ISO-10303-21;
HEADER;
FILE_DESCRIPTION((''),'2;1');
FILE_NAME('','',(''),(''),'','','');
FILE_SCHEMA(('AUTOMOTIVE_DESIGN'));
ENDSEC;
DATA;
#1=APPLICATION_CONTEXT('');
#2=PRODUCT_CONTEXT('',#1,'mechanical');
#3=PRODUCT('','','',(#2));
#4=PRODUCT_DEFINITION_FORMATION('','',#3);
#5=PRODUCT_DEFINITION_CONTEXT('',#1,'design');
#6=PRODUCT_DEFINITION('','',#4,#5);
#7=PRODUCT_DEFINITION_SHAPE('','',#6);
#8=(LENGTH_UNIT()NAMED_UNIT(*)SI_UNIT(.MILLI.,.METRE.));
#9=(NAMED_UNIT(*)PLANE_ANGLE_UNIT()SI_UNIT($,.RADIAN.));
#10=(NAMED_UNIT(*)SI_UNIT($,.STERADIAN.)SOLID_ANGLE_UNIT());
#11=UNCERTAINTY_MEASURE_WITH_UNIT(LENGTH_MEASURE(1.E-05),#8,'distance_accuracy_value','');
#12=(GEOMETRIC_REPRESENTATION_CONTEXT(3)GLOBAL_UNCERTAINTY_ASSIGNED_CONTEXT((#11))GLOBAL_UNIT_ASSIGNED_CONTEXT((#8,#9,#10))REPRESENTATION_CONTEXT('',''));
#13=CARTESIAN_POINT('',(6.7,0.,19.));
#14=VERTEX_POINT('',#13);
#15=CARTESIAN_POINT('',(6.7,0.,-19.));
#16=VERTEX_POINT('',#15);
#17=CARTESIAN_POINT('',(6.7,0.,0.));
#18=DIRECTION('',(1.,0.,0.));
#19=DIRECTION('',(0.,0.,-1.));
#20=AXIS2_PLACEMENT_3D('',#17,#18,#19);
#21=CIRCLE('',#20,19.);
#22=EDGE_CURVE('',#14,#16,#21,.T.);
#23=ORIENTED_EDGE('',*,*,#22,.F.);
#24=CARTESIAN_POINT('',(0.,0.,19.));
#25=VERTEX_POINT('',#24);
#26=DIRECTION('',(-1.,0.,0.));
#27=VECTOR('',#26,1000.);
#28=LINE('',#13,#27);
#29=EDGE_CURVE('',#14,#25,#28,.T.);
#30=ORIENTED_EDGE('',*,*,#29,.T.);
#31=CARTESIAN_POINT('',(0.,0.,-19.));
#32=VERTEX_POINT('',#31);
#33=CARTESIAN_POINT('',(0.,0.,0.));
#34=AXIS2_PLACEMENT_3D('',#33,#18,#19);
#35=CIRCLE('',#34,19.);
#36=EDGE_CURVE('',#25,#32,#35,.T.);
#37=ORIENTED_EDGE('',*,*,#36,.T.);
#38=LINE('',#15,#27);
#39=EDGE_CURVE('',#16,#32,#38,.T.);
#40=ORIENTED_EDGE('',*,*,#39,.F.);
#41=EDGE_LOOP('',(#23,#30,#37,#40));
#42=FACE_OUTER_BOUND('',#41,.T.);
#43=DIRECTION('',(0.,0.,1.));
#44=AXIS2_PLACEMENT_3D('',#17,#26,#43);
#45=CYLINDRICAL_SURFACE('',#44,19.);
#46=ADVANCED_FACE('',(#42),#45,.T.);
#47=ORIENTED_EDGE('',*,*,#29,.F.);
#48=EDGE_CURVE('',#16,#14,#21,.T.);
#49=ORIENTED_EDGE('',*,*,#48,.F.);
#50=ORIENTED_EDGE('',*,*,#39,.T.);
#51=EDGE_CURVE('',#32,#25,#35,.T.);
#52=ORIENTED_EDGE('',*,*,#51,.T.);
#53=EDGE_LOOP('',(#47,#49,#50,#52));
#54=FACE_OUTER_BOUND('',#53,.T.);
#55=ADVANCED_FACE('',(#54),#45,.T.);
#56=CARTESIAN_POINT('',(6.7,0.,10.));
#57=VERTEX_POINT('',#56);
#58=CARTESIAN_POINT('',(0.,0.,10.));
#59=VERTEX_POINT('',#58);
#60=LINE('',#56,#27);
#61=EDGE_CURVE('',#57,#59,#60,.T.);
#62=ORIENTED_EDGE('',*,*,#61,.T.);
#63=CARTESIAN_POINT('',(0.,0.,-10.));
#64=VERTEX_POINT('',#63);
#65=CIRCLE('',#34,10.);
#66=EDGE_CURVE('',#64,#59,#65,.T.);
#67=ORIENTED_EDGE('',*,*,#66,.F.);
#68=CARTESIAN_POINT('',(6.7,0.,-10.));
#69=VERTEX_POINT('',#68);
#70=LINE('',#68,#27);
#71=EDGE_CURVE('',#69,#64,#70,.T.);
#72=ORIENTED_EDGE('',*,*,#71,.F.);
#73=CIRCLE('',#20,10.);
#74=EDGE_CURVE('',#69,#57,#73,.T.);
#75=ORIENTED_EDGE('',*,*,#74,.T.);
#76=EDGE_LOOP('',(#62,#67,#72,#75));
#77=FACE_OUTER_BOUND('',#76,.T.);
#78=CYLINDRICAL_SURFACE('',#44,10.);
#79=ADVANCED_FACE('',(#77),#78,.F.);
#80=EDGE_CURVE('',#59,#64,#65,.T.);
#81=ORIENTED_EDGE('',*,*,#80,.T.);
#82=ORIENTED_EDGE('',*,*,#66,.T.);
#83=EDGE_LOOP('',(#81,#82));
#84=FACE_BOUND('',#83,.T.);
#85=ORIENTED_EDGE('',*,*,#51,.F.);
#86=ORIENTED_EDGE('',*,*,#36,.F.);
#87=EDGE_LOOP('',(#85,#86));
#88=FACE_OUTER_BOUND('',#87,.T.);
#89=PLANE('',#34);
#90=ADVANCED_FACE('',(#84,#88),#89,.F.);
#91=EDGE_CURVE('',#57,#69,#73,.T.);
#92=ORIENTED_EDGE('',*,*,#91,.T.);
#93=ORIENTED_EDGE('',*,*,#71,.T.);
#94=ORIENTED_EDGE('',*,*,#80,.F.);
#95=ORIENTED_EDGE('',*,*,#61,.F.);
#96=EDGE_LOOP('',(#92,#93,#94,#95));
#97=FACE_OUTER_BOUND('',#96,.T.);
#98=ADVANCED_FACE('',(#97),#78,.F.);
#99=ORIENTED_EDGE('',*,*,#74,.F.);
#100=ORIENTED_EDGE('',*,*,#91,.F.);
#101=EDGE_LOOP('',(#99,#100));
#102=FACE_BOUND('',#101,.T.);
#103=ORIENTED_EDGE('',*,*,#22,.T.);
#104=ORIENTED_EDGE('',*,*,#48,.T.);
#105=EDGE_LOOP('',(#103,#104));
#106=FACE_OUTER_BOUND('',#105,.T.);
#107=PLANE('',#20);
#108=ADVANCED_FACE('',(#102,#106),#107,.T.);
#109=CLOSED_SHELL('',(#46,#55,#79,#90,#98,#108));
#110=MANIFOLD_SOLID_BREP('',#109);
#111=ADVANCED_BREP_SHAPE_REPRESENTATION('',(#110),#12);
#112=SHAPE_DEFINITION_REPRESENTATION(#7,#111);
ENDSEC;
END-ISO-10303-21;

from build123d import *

# Parameters (mm, degrees)
SKETCH1_R           = 19
SKETCH1_R_2         = 10
BOSS_EXTRUDE1_DEPTH = 6.7


with BuildPart() as part:
    # Sketch1 → Boss-Extrude1 (new body)
    with BuildSketch(Plane(origin=(0, 0, 0), x_dir=(0, 0, -1), z_dir=(1, 0, 0))):
        Circle(SKETCH1_R)
        Circle(SKETCH1_R_2, mode=Mode.SUBTRACT)
    extrude(amount=BOSS_EXTRUDE1_DEPTH)


solid = part.part
